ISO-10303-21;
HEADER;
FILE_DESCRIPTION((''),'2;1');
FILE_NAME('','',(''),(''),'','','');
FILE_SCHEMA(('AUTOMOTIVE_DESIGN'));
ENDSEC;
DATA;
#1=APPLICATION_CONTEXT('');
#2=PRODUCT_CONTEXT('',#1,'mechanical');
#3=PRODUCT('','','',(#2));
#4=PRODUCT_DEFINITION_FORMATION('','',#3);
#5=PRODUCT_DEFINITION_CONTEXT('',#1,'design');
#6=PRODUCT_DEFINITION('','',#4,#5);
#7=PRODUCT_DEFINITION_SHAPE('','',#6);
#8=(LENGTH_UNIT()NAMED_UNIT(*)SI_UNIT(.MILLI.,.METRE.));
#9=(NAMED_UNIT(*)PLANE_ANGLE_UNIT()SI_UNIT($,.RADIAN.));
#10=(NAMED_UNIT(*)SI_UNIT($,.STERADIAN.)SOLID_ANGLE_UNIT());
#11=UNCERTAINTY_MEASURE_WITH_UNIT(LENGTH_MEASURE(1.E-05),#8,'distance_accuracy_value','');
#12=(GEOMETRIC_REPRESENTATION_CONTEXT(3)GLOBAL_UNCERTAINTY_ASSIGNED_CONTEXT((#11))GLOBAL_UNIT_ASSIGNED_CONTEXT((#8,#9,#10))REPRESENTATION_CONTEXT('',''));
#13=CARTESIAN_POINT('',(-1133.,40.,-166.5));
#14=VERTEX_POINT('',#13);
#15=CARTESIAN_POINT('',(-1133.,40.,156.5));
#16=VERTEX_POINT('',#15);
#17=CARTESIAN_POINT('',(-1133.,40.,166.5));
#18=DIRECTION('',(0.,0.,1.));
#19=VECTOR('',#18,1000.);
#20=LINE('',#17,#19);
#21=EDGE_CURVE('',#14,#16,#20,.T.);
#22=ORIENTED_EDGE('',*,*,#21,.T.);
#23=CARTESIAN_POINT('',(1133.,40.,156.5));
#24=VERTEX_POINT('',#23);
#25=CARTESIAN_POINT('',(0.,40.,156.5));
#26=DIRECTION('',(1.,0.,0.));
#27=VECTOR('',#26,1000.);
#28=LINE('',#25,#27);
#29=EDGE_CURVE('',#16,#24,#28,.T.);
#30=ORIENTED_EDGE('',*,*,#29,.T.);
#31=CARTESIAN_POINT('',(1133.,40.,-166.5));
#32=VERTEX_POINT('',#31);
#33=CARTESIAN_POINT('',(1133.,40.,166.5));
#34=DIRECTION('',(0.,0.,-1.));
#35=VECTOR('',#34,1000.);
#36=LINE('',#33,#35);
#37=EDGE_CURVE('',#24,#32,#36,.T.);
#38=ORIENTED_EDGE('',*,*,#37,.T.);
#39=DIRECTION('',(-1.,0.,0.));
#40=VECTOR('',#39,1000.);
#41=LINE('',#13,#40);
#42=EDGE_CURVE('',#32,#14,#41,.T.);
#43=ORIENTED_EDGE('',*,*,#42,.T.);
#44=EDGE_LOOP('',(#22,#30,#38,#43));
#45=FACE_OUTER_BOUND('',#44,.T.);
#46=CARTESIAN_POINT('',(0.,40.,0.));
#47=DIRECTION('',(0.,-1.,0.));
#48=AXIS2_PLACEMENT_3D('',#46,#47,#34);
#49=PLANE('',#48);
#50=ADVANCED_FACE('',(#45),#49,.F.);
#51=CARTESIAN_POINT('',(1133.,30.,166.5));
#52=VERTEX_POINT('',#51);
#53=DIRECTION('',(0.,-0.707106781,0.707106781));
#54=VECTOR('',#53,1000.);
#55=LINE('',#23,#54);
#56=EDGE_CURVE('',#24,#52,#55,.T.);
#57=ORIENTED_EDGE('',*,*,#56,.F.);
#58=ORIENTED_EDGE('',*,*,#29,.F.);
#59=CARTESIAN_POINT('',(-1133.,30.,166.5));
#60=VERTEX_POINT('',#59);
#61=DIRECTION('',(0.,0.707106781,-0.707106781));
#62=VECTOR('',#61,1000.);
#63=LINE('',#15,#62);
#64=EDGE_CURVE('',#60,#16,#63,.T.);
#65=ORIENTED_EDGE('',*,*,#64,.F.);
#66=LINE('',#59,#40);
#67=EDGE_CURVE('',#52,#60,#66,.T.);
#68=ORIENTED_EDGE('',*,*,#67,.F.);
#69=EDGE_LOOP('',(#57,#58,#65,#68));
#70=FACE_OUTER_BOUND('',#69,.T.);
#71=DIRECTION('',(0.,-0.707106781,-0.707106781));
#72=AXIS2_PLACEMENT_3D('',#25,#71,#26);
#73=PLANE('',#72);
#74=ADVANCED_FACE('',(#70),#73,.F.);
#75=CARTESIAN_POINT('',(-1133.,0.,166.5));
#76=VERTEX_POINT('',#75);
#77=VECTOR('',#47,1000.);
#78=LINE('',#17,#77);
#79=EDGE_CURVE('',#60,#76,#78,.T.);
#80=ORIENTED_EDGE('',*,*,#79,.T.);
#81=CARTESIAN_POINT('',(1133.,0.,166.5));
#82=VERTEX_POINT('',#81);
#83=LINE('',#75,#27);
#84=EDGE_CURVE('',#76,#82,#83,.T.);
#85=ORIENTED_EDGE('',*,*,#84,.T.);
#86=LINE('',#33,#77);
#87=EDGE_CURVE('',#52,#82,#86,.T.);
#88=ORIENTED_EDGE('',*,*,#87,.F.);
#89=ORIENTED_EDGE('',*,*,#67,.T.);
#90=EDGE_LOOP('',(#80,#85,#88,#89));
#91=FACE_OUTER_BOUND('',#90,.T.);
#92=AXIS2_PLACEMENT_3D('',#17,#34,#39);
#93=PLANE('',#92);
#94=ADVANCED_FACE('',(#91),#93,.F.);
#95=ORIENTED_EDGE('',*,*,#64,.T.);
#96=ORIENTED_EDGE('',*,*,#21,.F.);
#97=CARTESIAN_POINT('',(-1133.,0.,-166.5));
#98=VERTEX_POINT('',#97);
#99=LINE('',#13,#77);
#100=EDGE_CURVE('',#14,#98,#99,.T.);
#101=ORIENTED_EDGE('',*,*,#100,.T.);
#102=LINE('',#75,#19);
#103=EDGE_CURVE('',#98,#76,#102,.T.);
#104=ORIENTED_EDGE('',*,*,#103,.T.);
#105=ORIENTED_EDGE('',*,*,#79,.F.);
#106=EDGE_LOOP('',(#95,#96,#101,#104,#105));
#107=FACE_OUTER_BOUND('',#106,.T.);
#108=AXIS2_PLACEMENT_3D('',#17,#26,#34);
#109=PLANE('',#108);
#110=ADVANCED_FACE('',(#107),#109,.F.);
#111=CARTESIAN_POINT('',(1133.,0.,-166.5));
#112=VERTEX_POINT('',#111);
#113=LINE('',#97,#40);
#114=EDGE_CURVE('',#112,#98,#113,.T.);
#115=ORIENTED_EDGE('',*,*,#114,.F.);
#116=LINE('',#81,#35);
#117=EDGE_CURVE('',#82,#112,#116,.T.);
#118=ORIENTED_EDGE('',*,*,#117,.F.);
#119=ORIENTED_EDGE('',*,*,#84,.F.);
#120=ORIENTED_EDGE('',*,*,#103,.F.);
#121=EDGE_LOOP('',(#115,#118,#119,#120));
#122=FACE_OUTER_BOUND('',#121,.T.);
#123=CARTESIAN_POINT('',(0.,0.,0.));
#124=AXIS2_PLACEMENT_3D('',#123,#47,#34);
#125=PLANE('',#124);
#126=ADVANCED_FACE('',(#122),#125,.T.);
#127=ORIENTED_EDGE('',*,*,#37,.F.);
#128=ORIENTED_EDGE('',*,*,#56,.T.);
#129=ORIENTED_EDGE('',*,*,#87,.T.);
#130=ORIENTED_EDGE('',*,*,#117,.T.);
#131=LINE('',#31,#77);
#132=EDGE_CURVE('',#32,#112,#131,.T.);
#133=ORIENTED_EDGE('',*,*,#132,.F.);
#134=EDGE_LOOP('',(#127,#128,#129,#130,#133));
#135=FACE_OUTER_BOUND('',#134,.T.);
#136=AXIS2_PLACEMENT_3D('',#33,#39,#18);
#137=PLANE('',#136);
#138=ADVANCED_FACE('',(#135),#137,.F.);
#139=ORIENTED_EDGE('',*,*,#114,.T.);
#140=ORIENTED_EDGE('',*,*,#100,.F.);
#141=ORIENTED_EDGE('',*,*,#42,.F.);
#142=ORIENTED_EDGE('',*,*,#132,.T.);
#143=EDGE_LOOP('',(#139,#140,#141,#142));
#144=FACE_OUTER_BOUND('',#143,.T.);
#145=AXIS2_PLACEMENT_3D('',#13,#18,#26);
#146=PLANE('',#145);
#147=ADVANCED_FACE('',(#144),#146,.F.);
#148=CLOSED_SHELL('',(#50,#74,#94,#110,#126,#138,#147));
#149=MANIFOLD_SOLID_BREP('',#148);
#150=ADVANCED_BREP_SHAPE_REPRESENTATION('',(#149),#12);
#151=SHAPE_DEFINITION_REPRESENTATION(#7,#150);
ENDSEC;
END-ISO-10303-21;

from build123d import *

# Parameters (mm, degrees)
SKETCH_1_W      = 2266
SKETCH_1_H      = 333
EXTRUDE_1_DEPTH = 40
CHAMFER_1_SIZE  = 10


with BuildPart() as part:
    # 草图1 → 凸台-拉伸1 (new body)
    with BuildSketch(Plane(origin=(0, 0, 0), x_dir=(1, 0, 0), z_dir=(0, 1, 0))):
        Rectangle(SKETCH_1_W, SKETCH_1_H)
    extrude(amount=EXTRUDE_1_DEPTH)

    # 倒角1
    chamfer_1_edges = [part.edges().sort_by_distance(p)[0] for p in [
        (0, 40, 166.5),
    ]]
    chamfer(chamfer_1_edges, length=CHAMFER_1_SIZE)


solid = part.part
